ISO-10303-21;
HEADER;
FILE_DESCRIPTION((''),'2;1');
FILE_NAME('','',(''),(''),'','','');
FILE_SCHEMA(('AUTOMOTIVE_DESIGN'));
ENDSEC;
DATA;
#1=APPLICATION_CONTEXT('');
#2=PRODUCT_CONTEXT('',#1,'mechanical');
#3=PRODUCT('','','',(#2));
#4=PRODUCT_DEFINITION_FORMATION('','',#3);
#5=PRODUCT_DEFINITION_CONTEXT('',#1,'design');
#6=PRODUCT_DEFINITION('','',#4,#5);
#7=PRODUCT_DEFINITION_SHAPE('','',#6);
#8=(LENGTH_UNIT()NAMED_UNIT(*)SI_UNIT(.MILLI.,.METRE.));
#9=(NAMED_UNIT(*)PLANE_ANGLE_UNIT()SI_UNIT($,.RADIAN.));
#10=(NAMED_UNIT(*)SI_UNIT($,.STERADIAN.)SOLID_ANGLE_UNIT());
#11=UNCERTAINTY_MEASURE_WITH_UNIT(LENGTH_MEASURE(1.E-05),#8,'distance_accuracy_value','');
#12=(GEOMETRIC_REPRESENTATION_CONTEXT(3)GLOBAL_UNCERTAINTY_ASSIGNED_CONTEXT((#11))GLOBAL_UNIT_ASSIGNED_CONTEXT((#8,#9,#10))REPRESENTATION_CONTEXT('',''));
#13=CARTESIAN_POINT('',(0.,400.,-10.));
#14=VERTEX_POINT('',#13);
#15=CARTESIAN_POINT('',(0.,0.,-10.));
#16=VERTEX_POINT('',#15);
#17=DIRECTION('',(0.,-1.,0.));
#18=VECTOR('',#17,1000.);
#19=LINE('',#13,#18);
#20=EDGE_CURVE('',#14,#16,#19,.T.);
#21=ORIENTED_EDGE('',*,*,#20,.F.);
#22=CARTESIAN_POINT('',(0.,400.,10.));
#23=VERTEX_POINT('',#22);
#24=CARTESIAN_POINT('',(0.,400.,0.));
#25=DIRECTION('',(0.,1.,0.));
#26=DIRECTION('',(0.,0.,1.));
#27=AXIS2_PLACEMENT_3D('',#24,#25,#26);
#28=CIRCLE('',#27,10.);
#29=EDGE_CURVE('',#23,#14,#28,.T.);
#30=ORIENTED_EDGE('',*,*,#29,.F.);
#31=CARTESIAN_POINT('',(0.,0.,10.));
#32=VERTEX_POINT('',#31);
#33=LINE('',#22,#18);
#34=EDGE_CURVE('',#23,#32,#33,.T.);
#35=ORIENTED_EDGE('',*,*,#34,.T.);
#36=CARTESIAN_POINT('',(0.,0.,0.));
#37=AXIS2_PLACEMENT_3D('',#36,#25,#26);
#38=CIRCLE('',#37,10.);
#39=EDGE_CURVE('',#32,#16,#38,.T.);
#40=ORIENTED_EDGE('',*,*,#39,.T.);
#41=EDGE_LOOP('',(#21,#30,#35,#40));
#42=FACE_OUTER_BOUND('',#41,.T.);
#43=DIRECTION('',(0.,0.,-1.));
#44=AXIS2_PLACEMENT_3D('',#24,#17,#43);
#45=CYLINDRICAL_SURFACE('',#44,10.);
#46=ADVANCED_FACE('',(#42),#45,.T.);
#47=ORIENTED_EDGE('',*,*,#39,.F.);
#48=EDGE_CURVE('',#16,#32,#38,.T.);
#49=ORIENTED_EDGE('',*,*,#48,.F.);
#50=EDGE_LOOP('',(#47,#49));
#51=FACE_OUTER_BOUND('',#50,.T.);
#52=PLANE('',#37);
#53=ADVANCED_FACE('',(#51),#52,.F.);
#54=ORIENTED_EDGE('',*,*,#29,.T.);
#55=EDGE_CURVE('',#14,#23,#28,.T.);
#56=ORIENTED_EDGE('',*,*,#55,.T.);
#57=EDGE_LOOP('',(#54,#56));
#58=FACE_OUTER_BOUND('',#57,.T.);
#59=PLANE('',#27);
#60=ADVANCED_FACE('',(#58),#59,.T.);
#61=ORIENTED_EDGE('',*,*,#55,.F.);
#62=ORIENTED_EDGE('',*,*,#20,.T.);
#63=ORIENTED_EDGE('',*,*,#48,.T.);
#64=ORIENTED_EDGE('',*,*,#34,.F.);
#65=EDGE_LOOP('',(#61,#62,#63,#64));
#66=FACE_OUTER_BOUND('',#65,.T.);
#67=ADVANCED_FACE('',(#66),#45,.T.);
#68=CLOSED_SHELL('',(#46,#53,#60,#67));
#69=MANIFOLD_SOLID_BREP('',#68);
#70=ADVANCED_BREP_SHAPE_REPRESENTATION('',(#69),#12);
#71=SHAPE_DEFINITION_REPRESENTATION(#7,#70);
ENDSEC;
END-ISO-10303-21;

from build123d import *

# Parameters (mm, degrees)
SKETCH1_R           = 10
BOSS_EXTRUDE1_DEPTH = 400


with BuildPart() as part:
    # Sketch1 → Boss-Extrude1 (new body)
    with BuildSketch(Plane(origin=(0, 0, 0), x_dir=(1, 0, 0), z_dir=(0, 1, 0))):
        with Locations(Location((0, 0, 0), (0, 0, 270))):
            Circle(SKETCH1_R)
    extrude(amount=BOSS_EXTRUDE1_DEPTH)


solid = part.part
